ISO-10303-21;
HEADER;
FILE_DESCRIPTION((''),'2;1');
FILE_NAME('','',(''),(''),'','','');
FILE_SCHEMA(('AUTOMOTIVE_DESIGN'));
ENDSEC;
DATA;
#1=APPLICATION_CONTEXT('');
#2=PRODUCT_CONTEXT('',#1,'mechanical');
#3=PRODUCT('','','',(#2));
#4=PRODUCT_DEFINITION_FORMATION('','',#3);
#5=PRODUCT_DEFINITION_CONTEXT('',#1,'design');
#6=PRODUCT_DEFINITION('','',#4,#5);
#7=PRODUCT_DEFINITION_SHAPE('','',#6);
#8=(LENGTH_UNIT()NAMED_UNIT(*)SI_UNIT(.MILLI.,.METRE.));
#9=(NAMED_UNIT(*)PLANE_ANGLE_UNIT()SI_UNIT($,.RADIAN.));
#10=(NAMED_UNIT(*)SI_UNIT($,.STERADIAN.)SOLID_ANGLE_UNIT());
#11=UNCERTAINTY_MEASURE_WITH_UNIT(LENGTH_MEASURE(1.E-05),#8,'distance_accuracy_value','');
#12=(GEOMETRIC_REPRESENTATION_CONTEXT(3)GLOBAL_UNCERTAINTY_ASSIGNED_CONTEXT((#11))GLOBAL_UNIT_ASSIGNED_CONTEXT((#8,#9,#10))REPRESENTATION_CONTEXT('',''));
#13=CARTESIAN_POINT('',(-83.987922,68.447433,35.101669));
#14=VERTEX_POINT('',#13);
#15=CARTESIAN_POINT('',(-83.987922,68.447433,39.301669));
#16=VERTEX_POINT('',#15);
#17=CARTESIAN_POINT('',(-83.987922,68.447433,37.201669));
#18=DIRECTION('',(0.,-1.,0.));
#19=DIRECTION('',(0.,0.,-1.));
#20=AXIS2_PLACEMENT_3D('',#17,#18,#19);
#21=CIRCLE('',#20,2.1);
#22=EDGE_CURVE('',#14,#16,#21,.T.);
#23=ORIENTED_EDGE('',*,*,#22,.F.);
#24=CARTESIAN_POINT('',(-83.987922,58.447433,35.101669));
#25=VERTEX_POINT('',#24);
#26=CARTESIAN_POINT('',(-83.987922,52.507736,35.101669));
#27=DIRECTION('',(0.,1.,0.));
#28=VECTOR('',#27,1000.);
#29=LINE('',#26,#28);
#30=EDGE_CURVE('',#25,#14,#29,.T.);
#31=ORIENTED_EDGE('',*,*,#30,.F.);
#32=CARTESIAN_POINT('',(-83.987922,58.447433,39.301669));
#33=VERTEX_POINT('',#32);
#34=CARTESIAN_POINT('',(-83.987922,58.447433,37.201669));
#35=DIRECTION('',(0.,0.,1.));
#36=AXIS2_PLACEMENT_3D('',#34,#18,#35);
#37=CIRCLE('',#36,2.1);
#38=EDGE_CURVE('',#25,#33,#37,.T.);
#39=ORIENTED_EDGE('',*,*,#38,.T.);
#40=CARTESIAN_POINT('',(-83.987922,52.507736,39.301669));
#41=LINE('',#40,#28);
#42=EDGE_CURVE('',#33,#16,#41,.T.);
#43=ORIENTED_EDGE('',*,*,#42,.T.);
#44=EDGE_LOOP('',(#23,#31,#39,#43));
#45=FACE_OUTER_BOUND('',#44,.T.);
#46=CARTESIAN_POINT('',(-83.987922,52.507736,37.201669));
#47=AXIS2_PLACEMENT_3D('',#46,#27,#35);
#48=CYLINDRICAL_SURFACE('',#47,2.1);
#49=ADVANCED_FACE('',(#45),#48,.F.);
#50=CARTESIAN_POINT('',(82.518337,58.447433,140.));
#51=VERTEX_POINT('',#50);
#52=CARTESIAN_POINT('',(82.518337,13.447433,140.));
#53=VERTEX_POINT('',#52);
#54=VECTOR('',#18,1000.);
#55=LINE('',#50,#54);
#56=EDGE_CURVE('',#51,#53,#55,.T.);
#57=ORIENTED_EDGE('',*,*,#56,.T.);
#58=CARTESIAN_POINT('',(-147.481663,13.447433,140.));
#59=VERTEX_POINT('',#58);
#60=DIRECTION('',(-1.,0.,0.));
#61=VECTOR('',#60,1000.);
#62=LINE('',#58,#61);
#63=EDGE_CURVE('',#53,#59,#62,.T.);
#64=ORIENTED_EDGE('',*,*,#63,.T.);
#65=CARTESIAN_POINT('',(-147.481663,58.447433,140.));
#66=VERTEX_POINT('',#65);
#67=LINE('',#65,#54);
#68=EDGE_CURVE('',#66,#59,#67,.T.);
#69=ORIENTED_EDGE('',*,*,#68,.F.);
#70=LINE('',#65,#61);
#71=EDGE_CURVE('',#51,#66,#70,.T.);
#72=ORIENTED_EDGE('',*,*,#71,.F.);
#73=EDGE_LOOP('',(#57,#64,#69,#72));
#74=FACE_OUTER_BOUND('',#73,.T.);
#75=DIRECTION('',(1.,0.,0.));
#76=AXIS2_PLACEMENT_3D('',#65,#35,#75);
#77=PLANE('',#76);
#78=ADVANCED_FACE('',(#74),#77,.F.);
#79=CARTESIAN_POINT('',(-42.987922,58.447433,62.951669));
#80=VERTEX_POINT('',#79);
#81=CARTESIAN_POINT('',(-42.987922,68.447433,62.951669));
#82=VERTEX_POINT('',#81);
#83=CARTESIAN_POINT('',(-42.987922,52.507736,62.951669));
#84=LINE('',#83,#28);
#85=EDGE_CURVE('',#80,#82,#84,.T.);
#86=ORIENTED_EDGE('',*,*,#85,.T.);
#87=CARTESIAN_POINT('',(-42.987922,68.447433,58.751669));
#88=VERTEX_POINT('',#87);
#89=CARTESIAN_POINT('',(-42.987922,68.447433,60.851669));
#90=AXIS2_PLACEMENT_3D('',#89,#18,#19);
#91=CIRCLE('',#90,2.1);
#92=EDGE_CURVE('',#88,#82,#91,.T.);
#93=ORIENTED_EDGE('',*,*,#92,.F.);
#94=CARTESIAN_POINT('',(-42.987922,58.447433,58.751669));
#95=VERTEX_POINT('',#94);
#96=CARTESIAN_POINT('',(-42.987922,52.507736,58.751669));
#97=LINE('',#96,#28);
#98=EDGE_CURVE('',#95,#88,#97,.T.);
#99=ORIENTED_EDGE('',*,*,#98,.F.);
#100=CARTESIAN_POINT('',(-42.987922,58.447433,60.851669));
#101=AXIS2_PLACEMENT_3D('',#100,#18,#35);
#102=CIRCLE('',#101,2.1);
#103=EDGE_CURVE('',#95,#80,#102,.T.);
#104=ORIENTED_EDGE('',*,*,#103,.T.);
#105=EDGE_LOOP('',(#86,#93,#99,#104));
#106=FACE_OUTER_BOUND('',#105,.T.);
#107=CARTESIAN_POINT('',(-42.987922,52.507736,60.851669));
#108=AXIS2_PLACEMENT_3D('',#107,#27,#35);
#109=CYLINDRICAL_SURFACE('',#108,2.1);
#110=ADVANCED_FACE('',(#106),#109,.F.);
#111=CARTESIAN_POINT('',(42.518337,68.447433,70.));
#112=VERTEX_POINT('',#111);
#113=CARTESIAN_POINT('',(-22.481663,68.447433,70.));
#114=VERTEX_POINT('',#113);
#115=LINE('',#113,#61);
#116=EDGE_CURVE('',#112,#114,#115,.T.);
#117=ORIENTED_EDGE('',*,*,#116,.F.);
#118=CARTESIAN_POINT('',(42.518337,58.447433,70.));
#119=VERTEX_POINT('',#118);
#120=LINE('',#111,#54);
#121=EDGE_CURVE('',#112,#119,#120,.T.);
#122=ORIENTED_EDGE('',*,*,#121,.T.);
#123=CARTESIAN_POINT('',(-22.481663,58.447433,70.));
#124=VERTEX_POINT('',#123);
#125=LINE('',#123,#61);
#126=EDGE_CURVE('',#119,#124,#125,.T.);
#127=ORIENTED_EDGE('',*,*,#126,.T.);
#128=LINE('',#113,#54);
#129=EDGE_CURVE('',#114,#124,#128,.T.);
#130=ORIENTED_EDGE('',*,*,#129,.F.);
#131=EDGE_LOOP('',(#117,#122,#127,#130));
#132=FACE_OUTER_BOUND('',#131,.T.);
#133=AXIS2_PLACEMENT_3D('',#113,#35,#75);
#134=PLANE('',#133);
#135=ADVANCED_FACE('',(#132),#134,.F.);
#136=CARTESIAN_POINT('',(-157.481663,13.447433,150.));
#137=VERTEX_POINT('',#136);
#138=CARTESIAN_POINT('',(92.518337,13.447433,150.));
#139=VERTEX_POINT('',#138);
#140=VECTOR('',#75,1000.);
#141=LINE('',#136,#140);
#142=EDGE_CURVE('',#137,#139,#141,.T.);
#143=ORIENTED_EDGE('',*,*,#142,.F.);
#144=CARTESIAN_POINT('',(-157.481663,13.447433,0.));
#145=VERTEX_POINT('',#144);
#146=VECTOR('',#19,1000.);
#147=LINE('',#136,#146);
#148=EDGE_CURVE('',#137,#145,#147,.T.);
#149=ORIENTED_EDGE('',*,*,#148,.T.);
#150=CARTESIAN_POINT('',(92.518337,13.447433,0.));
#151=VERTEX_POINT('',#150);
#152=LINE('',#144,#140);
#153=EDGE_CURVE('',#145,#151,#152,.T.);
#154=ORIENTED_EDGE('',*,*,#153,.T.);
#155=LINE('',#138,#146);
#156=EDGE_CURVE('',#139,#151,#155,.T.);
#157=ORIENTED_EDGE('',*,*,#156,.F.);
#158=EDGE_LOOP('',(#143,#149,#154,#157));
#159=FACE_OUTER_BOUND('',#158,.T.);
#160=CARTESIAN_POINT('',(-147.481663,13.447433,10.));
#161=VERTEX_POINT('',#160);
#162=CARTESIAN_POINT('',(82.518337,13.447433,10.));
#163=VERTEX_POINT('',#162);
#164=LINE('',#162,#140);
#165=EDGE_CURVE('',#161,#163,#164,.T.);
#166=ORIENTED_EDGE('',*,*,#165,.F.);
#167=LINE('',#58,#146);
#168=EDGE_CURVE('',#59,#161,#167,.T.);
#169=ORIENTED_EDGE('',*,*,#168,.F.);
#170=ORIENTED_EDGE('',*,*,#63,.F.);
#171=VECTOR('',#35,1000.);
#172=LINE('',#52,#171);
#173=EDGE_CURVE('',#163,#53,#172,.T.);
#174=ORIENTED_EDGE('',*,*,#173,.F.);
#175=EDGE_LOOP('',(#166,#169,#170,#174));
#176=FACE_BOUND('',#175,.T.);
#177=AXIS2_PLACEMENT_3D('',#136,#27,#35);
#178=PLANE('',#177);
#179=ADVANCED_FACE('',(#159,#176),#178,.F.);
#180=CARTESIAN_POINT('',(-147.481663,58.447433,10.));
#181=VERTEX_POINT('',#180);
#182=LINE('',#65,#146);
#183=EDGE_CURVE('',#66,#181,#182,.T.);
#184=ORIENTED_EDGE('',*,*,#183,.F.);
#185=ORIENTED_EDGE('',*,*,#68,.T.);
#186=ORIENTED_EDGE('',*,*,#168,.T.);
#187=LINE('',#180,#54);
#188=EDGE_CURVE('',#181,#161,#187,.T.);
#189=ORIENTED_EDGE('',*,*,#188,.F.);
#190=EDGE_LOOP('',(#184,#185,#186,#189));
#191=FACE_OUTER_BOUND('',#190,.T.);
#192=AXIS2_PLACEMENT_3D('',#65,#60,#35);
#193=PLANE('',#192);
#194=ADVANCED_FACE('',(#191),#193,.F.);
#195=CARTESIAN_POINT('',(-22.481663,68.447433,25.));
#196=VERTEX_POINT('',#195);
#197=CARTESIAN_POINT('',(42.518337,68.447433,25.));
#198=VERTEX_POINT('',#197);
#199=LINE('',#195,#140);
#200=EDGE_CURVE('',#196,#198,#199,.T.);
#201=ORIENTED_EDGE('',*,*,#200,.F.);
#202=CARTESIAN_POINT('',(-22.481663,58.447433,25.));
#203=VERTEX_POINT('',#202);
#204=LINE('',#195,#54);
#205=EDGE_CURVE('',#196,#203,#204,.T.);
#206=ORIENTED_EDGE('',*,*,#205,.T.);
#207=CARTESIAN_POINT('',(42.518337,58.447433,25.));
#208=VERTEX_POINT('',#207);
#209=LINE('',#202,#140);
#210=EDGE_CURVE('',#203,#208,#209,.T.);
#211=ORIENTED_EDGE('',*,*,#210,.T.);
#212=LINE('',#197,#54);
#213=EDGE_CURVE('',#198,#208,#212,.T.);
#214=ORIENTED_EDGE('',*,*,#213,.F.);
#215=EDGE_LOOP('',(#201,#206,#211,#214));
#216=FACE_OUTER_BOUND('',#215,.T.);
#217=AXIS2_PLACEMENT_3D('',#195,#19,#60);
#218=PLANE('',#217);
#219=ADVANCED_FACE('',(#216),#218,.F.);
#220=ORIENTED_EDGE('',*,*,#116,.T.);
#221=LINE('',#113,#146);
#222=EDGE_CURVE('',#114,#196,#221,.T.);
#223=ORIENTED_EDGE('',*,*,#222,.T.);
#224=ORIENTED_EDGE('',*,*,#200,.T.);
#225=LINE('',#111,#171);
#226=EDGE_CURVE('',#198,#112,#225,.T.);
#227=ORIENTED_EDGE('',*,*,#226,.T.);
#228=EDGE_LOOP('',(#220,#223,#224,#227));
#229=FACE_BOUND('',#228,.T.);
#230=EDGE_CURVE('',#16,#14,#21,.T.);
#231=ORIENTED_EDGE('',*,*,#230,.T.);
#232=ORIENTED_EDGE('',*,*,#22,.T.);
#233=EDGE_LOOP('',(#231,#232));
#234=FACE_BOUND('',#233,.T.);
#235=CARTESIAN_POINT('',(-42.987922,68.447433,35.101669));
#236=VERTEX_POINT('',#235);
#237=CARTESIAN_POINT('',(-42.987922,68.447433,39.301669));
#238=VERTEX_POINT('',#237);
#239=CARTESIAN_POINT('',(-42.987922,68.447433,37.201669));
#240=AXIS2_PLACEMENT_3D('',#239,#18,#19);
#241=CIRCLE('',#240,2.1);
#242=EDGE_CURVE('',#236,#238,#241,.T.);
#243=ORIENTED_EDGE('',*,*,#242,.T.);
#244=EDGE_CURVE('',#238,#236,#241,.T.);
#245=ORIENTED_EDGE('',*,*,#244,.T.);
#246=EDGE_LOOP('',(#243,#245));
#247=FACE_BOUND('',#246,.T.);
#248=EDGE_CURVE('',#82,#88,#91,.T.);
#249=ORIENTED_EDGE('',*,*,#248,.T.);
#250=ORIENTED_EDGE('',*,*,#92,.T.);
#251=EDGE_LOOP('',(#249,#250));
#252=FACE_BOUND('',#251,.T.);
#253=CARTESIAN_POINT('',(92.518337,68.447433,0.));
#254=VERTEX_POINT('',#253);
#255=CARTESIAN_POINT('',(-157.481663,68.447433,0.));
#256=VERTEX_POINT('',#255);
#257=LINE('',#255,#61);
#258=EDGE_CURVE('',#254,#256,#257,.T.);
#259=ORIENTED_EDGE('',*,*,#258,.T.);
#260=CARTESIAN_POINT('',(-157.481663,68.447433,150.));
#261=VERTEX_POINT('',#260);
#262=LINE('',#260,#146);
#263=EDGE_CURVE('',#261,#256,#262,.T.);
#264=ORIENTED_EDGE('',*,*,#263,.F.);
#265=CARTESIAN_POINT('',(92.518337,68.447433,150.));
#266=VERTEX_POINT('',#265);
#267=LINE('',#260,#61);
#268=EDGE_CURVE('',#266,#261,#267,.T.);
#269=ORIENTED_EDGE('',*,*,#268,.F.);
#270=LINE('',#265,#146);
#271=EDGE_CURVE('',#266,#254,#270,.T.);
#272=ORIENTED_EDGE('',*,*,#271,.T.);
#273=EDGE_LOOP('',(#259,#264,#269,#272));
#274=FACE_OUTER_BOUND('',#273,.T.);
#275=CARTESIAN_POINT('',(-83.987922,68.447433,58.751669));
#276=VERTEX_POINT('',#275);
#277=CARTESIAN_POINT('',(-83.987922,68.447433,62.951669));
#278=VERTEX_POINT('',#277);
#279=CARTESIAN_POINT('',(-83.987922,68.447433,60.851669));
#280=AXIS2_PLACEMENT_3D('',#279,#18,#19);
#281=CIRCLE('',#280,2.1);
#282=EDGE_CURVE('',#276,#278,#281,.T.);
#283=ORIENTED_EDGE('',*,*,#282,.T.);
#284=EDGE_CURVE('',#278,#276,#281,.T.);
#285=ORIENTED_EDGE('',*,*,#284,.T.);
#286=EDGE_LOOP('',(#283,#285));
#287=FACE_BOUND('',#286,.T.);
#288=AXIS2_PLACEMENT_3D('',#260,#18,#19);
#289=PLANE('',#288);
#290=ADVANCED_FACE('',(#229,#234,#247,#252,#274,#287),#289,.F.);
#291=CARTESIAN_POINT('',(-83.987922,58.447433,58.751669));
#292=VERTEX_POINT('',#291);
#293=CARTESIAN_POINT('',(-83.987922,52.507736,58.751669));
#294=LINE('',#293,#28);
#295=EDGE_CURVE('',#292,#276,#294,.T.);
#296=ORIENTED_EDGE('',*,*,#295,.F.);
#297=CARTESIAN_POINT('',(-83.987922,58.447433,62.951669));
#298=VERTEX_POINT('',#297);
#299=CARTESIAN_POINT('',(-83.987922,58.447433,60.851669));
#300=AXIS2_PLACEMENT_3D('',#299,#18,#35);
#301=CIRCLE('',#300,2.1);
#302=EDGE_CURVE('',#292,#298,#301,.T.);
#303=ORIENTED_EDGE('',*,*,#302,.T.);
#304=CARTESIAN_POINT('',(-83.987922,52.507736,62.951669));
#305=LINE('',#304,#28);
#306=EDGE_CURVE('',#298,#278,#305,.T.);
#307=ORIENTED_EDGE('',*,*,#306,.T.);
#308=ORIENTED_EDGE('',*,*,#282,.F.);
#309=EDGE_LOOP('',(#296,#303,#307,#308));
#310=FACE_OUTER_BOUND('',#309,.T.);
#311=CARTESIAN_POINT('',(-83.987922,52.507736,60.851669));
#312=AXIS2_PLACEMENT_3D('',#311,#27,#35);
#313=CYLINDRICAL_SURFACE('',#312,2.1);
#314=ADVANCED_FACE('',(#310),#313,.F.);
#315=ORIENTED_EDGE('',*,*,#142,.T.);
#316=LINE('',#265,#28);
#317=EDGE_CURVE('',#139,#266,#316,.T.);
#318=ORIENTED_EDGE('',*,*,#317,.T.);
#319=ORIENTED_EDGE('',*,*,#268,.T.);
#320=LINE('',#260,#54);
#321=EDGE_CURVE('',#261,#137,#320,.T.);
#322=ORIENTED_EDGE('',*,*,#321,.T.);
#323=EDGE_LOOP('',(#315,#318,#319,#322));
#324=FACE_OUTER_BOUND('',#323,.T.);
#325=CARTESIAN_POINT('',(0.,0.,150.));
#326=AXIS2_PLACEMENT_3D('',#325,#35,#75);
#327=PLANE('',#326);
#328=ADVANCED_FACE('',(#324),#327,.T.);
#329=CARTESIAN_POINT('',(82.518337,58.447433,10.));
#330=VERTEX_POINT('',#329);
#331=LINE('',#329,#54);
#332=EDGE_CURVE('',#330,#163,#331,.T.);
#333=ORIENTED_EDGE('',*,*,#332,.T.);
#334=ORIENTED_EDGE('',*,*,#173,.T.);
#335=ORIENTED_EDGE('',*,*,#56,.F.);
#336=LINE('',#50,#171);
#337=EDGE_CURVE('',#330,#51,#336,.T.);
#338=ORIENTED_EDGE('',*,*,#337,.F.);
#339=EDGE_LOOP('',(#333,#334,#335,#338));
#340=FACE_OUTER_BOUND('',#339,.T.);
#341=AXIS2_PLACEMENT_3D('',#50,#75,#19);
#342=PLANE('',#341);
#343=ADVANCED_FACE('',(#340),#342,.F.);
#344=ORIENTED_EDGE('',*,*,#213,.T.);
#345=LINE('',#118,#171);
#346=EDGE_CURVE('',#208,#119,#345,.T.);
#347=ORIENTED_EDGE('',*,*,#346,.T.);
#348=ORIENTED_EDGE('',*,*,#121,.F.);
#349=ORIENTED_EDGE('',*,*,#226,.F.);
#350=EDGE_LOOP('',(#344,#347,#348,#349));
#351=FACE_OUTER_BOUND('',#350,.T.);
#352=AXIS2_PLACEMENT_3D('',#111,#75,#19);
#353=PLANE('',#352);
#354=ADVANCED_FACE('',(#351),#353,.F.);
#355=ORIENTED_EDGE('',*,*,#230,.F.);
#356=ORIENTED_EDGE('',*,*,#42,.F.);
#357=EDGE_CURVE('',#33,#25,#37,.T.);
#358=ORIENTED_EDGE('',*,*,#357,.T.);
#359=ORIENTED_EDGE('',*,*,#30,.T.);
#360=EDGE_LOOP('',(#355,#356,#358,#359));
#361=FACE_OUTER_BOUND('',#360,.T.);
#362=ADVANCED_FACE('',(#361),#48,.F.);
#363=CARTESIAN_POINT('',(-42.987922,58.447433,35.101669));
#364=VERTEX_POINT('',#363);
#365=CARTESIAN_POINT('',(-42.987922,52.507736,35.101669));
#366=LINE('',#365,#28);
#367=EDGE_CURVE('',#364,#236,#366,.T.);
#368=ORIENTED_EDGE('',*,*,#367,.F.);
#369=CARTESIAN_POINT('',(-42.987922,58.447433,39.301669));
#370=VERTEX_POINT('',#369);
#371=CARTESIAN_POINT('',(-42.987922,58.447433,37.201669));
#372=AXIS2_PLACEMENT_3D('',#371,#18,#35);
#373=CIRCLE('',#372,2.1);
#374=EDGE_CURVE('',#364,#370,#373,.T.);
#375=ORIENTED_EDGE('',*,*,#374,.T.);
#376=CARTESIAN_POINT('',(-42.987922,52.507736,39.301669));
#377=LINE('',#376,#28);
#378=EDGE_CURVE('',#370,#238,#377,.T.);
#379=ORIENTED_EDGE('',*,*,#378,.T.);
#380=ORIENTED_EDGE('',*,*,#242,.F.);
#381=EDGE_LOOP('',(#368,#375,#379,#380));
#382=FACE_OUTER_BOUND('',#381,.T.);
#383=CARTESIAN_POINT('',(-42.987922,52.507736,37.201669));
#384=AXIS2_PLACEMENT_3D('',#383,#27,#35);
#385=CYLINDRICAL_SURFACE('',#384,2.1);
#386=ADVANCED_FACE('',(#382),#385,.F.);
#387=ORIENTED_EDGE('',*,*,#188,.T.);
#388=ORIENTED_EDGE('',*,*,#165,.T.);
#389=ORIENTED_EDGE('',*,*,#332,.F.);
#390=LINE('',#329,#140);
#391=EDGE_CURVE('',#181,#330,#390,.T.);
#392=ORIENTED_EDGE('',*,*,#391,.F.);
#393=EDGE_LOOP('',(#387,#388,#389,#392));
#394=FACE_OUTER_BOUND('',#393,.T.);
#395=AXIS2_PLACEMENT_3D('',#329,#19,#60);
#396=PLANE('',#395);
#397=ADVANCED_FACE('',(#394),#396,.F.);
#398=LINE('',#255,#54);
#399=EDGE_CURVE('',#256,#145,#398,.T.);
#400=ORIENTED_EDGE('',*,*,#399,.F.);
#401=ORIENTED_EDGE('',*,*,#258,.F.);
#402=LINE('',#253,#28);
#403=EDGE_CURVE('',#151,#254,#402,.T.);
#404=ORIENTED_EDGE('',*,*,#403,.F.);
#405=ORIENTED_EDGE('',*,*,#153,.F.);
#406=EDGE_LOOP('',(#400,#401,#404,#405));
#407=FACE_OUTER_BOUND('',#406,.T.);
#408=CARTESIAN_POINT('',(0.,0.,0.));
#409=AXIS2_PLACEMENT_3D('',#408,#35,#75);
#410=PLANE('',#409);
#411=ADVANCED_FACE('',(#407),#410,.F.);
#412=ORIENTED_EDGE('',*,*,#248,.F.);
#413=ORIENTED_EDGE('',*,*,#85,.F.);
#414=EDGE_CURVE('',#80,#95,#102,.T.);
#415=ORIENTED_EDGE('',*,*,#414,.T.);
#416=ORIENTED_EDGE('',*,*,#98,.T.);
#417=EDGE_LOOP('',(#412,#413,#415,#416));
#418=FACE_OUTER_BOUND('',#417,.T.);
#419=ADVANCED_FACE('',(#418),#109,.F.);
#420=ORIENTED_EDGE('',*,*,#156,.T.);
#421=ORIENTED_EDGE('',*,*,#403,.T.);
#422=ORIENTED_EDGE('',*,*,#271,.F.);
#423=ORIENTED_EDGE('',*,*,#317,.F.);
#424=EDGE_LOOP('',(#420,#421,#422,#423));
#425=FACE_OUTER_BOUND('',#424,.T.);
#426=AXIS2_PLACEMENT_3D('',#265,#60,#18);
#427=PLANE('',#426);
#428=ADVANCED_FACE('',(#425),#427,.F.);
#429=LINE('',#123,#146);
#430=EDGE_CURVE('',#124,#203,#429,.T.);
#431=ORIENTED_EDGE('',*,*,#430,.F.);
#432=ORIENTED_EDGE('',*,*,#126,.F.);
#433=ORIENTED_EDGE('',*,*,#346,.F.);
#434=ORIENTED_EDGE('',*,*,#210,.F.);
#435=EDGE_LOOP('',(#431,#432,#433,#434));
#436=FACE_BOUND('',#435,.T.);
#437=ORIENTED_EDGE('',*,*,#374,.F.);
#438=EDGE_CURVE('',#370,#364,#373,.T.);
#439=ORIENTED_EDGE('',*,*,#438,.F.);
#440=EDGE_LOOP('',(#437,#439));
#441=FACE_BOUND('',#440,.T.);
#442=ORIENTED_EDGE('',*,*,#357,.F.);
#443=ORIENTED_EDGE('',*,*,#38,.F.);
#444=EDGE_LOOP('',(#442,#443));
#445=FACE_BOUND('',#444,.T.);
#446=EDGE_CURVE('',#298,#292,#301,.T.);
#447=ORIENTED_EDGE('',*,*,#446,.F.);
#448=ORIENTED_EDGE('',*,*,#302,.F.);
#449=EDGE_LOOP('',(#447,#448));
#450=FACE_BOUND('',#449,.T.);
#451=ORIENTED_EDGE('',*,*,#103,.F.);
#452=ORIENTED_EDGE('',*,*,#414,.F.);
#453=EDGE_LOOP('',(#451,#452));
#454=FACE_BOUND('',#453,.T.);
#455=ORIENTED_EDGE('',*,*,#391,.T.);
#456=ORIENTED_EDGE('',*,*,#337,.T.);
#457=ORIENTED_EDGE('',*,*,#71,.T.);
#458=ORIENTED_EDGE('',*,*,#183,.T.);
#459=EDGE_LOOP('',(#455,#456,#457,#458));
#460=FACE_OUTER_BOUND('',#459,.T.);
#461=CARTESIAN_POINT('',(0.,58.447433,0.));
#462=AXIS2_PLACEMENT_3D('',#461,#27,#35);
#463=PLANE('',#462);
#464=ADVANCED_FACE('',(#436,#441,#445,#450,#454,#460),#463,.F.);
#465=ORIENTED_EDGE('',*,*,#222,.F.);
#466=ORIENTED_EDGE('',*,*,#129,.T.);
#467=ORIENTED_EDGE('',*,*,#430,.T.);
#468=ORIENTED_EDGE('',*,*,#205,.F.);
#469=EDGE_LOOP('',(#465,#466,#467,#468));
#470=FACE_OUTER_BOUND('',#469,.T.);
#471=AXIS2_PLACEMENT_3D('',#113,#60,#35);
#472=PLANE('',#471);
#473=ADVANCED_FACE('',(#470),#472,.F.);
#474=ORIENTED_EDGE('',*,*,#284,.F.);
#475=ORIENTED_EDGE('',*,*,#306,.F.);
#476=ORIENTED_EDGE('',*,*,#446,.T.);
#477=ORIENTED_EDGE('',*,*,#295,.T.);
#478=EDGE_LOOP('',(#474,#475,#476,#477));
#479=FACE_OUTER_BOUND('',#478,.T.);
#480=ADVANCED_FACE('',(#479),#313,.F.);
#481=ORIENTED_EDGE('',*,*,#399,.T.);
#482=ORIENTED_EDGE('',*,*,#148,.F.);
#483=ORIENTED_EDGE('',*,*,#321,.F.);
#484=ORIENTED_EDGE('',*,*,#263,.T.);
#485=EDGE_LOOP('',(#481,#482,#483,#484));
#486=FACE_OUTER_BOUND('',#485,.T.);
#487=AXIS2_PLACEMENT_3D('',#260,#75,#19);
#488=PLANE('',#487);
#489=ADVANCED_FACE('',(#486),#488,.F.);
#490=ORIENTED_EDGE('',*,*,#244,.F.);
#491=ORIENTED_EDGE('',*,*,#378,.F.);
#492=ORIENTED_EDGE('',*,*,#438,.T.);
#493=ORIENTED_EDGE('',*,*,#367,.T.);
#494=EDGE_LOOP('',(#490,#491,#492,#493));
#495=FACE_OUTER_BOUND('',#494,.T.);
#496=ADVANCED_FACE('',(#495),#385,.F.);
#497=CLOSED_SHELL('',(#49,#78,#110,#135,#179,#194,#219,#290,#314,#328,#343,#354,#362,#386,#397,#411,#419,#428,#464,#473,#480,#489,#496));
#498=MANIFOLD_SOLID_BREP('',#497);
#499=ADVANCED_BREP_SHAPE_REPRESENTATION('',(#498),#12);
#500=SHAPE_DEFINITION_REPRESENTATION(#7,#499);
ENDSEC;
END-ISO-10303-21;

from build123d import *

# Parameters (mm, degrees)
SKETCH_1_W          = 250
SKETCH_1_H          = 55
EXTRUDE_1_DEPTH     = 150
SKETCH_2_W          = 230
SKETCH_2_H          = 130
CUT_EXTRUDE_1_DEPTH = 45
SKETCH_4_W          = 65
SKETCH_4_H          = 45
CUT_EXTRUDE_2_DEPTH = 223.093390385
SKETCH_10_R         = 2.1
CUT_EXTRUDE_8_DEPTH = 17.7


with BuildPart() as part:
    # 草图1 → 凸台-拉伸1 (new body)
    with BuildSketch(Plane.XY):
        with Locations((-32.481662592, 40.947432763)):
            Rectangle(SKETCH_1_W, SKETCH_1_H)
    extrude(amount=EXTRUDE_1_DEPTH)

    # 草图2 → 切除-拉伸1 (cut)
    with BuildSketch(Plane.XZ.offset(-13.447432763)):
        with Locations((-32.481662592, 75)):
            Rectangle(SKETCH_2_W, SKETCH_2_H)
    extrude(amount=-CUT_EXTRUDE_1_DEPTH, mode=Mode.SUBTRACT)

    # 草图4 → 切除-拉伸2 (cut, through all)
    with BuildSketch(Plane.XZ.offset(-58.447432763)):
        with Locations((10.018337408, 47.5)):
            Rectangle(SKETCH_4_W, SKETCH_4_H)
    extrude(amount=-CUT_EXTRUDE_2_DEPTH, mode=Mode.SUBTRACT)

    # 草图10 → 切除-拉伸8 (cut)
    with BuildSketch(Plane(origin=(971.262341276, 76.147432763, 1019.143932915), x_dir=(1, 0, 0), z_dir=(0, 1, 0))):
        with Locations(Location((-1055.250263055, 981.942263912, 0), (0, 0, 270))):
            Circle(SKETCH_10_R)
        with Locations(Location((-1055.250263055, 958.292263912, 0), (0, 0, 270))):
            Circle(SKETCH_10_R)
        with Locations(Location((-1014.250263055, 958.292263912, 0), (0, 0, 270))):
            Circle(SKETCH_10_R)
        with Locations(Location((-1014.250263055, 981.942263912, 0), (0, 0, 270))):
            Circle(SKETCH_10_R)
    extrude(amount=-CUT_EXTRUDE_8_DEPTH, mode=Mode.SUBTRACT)


solid = part.part
